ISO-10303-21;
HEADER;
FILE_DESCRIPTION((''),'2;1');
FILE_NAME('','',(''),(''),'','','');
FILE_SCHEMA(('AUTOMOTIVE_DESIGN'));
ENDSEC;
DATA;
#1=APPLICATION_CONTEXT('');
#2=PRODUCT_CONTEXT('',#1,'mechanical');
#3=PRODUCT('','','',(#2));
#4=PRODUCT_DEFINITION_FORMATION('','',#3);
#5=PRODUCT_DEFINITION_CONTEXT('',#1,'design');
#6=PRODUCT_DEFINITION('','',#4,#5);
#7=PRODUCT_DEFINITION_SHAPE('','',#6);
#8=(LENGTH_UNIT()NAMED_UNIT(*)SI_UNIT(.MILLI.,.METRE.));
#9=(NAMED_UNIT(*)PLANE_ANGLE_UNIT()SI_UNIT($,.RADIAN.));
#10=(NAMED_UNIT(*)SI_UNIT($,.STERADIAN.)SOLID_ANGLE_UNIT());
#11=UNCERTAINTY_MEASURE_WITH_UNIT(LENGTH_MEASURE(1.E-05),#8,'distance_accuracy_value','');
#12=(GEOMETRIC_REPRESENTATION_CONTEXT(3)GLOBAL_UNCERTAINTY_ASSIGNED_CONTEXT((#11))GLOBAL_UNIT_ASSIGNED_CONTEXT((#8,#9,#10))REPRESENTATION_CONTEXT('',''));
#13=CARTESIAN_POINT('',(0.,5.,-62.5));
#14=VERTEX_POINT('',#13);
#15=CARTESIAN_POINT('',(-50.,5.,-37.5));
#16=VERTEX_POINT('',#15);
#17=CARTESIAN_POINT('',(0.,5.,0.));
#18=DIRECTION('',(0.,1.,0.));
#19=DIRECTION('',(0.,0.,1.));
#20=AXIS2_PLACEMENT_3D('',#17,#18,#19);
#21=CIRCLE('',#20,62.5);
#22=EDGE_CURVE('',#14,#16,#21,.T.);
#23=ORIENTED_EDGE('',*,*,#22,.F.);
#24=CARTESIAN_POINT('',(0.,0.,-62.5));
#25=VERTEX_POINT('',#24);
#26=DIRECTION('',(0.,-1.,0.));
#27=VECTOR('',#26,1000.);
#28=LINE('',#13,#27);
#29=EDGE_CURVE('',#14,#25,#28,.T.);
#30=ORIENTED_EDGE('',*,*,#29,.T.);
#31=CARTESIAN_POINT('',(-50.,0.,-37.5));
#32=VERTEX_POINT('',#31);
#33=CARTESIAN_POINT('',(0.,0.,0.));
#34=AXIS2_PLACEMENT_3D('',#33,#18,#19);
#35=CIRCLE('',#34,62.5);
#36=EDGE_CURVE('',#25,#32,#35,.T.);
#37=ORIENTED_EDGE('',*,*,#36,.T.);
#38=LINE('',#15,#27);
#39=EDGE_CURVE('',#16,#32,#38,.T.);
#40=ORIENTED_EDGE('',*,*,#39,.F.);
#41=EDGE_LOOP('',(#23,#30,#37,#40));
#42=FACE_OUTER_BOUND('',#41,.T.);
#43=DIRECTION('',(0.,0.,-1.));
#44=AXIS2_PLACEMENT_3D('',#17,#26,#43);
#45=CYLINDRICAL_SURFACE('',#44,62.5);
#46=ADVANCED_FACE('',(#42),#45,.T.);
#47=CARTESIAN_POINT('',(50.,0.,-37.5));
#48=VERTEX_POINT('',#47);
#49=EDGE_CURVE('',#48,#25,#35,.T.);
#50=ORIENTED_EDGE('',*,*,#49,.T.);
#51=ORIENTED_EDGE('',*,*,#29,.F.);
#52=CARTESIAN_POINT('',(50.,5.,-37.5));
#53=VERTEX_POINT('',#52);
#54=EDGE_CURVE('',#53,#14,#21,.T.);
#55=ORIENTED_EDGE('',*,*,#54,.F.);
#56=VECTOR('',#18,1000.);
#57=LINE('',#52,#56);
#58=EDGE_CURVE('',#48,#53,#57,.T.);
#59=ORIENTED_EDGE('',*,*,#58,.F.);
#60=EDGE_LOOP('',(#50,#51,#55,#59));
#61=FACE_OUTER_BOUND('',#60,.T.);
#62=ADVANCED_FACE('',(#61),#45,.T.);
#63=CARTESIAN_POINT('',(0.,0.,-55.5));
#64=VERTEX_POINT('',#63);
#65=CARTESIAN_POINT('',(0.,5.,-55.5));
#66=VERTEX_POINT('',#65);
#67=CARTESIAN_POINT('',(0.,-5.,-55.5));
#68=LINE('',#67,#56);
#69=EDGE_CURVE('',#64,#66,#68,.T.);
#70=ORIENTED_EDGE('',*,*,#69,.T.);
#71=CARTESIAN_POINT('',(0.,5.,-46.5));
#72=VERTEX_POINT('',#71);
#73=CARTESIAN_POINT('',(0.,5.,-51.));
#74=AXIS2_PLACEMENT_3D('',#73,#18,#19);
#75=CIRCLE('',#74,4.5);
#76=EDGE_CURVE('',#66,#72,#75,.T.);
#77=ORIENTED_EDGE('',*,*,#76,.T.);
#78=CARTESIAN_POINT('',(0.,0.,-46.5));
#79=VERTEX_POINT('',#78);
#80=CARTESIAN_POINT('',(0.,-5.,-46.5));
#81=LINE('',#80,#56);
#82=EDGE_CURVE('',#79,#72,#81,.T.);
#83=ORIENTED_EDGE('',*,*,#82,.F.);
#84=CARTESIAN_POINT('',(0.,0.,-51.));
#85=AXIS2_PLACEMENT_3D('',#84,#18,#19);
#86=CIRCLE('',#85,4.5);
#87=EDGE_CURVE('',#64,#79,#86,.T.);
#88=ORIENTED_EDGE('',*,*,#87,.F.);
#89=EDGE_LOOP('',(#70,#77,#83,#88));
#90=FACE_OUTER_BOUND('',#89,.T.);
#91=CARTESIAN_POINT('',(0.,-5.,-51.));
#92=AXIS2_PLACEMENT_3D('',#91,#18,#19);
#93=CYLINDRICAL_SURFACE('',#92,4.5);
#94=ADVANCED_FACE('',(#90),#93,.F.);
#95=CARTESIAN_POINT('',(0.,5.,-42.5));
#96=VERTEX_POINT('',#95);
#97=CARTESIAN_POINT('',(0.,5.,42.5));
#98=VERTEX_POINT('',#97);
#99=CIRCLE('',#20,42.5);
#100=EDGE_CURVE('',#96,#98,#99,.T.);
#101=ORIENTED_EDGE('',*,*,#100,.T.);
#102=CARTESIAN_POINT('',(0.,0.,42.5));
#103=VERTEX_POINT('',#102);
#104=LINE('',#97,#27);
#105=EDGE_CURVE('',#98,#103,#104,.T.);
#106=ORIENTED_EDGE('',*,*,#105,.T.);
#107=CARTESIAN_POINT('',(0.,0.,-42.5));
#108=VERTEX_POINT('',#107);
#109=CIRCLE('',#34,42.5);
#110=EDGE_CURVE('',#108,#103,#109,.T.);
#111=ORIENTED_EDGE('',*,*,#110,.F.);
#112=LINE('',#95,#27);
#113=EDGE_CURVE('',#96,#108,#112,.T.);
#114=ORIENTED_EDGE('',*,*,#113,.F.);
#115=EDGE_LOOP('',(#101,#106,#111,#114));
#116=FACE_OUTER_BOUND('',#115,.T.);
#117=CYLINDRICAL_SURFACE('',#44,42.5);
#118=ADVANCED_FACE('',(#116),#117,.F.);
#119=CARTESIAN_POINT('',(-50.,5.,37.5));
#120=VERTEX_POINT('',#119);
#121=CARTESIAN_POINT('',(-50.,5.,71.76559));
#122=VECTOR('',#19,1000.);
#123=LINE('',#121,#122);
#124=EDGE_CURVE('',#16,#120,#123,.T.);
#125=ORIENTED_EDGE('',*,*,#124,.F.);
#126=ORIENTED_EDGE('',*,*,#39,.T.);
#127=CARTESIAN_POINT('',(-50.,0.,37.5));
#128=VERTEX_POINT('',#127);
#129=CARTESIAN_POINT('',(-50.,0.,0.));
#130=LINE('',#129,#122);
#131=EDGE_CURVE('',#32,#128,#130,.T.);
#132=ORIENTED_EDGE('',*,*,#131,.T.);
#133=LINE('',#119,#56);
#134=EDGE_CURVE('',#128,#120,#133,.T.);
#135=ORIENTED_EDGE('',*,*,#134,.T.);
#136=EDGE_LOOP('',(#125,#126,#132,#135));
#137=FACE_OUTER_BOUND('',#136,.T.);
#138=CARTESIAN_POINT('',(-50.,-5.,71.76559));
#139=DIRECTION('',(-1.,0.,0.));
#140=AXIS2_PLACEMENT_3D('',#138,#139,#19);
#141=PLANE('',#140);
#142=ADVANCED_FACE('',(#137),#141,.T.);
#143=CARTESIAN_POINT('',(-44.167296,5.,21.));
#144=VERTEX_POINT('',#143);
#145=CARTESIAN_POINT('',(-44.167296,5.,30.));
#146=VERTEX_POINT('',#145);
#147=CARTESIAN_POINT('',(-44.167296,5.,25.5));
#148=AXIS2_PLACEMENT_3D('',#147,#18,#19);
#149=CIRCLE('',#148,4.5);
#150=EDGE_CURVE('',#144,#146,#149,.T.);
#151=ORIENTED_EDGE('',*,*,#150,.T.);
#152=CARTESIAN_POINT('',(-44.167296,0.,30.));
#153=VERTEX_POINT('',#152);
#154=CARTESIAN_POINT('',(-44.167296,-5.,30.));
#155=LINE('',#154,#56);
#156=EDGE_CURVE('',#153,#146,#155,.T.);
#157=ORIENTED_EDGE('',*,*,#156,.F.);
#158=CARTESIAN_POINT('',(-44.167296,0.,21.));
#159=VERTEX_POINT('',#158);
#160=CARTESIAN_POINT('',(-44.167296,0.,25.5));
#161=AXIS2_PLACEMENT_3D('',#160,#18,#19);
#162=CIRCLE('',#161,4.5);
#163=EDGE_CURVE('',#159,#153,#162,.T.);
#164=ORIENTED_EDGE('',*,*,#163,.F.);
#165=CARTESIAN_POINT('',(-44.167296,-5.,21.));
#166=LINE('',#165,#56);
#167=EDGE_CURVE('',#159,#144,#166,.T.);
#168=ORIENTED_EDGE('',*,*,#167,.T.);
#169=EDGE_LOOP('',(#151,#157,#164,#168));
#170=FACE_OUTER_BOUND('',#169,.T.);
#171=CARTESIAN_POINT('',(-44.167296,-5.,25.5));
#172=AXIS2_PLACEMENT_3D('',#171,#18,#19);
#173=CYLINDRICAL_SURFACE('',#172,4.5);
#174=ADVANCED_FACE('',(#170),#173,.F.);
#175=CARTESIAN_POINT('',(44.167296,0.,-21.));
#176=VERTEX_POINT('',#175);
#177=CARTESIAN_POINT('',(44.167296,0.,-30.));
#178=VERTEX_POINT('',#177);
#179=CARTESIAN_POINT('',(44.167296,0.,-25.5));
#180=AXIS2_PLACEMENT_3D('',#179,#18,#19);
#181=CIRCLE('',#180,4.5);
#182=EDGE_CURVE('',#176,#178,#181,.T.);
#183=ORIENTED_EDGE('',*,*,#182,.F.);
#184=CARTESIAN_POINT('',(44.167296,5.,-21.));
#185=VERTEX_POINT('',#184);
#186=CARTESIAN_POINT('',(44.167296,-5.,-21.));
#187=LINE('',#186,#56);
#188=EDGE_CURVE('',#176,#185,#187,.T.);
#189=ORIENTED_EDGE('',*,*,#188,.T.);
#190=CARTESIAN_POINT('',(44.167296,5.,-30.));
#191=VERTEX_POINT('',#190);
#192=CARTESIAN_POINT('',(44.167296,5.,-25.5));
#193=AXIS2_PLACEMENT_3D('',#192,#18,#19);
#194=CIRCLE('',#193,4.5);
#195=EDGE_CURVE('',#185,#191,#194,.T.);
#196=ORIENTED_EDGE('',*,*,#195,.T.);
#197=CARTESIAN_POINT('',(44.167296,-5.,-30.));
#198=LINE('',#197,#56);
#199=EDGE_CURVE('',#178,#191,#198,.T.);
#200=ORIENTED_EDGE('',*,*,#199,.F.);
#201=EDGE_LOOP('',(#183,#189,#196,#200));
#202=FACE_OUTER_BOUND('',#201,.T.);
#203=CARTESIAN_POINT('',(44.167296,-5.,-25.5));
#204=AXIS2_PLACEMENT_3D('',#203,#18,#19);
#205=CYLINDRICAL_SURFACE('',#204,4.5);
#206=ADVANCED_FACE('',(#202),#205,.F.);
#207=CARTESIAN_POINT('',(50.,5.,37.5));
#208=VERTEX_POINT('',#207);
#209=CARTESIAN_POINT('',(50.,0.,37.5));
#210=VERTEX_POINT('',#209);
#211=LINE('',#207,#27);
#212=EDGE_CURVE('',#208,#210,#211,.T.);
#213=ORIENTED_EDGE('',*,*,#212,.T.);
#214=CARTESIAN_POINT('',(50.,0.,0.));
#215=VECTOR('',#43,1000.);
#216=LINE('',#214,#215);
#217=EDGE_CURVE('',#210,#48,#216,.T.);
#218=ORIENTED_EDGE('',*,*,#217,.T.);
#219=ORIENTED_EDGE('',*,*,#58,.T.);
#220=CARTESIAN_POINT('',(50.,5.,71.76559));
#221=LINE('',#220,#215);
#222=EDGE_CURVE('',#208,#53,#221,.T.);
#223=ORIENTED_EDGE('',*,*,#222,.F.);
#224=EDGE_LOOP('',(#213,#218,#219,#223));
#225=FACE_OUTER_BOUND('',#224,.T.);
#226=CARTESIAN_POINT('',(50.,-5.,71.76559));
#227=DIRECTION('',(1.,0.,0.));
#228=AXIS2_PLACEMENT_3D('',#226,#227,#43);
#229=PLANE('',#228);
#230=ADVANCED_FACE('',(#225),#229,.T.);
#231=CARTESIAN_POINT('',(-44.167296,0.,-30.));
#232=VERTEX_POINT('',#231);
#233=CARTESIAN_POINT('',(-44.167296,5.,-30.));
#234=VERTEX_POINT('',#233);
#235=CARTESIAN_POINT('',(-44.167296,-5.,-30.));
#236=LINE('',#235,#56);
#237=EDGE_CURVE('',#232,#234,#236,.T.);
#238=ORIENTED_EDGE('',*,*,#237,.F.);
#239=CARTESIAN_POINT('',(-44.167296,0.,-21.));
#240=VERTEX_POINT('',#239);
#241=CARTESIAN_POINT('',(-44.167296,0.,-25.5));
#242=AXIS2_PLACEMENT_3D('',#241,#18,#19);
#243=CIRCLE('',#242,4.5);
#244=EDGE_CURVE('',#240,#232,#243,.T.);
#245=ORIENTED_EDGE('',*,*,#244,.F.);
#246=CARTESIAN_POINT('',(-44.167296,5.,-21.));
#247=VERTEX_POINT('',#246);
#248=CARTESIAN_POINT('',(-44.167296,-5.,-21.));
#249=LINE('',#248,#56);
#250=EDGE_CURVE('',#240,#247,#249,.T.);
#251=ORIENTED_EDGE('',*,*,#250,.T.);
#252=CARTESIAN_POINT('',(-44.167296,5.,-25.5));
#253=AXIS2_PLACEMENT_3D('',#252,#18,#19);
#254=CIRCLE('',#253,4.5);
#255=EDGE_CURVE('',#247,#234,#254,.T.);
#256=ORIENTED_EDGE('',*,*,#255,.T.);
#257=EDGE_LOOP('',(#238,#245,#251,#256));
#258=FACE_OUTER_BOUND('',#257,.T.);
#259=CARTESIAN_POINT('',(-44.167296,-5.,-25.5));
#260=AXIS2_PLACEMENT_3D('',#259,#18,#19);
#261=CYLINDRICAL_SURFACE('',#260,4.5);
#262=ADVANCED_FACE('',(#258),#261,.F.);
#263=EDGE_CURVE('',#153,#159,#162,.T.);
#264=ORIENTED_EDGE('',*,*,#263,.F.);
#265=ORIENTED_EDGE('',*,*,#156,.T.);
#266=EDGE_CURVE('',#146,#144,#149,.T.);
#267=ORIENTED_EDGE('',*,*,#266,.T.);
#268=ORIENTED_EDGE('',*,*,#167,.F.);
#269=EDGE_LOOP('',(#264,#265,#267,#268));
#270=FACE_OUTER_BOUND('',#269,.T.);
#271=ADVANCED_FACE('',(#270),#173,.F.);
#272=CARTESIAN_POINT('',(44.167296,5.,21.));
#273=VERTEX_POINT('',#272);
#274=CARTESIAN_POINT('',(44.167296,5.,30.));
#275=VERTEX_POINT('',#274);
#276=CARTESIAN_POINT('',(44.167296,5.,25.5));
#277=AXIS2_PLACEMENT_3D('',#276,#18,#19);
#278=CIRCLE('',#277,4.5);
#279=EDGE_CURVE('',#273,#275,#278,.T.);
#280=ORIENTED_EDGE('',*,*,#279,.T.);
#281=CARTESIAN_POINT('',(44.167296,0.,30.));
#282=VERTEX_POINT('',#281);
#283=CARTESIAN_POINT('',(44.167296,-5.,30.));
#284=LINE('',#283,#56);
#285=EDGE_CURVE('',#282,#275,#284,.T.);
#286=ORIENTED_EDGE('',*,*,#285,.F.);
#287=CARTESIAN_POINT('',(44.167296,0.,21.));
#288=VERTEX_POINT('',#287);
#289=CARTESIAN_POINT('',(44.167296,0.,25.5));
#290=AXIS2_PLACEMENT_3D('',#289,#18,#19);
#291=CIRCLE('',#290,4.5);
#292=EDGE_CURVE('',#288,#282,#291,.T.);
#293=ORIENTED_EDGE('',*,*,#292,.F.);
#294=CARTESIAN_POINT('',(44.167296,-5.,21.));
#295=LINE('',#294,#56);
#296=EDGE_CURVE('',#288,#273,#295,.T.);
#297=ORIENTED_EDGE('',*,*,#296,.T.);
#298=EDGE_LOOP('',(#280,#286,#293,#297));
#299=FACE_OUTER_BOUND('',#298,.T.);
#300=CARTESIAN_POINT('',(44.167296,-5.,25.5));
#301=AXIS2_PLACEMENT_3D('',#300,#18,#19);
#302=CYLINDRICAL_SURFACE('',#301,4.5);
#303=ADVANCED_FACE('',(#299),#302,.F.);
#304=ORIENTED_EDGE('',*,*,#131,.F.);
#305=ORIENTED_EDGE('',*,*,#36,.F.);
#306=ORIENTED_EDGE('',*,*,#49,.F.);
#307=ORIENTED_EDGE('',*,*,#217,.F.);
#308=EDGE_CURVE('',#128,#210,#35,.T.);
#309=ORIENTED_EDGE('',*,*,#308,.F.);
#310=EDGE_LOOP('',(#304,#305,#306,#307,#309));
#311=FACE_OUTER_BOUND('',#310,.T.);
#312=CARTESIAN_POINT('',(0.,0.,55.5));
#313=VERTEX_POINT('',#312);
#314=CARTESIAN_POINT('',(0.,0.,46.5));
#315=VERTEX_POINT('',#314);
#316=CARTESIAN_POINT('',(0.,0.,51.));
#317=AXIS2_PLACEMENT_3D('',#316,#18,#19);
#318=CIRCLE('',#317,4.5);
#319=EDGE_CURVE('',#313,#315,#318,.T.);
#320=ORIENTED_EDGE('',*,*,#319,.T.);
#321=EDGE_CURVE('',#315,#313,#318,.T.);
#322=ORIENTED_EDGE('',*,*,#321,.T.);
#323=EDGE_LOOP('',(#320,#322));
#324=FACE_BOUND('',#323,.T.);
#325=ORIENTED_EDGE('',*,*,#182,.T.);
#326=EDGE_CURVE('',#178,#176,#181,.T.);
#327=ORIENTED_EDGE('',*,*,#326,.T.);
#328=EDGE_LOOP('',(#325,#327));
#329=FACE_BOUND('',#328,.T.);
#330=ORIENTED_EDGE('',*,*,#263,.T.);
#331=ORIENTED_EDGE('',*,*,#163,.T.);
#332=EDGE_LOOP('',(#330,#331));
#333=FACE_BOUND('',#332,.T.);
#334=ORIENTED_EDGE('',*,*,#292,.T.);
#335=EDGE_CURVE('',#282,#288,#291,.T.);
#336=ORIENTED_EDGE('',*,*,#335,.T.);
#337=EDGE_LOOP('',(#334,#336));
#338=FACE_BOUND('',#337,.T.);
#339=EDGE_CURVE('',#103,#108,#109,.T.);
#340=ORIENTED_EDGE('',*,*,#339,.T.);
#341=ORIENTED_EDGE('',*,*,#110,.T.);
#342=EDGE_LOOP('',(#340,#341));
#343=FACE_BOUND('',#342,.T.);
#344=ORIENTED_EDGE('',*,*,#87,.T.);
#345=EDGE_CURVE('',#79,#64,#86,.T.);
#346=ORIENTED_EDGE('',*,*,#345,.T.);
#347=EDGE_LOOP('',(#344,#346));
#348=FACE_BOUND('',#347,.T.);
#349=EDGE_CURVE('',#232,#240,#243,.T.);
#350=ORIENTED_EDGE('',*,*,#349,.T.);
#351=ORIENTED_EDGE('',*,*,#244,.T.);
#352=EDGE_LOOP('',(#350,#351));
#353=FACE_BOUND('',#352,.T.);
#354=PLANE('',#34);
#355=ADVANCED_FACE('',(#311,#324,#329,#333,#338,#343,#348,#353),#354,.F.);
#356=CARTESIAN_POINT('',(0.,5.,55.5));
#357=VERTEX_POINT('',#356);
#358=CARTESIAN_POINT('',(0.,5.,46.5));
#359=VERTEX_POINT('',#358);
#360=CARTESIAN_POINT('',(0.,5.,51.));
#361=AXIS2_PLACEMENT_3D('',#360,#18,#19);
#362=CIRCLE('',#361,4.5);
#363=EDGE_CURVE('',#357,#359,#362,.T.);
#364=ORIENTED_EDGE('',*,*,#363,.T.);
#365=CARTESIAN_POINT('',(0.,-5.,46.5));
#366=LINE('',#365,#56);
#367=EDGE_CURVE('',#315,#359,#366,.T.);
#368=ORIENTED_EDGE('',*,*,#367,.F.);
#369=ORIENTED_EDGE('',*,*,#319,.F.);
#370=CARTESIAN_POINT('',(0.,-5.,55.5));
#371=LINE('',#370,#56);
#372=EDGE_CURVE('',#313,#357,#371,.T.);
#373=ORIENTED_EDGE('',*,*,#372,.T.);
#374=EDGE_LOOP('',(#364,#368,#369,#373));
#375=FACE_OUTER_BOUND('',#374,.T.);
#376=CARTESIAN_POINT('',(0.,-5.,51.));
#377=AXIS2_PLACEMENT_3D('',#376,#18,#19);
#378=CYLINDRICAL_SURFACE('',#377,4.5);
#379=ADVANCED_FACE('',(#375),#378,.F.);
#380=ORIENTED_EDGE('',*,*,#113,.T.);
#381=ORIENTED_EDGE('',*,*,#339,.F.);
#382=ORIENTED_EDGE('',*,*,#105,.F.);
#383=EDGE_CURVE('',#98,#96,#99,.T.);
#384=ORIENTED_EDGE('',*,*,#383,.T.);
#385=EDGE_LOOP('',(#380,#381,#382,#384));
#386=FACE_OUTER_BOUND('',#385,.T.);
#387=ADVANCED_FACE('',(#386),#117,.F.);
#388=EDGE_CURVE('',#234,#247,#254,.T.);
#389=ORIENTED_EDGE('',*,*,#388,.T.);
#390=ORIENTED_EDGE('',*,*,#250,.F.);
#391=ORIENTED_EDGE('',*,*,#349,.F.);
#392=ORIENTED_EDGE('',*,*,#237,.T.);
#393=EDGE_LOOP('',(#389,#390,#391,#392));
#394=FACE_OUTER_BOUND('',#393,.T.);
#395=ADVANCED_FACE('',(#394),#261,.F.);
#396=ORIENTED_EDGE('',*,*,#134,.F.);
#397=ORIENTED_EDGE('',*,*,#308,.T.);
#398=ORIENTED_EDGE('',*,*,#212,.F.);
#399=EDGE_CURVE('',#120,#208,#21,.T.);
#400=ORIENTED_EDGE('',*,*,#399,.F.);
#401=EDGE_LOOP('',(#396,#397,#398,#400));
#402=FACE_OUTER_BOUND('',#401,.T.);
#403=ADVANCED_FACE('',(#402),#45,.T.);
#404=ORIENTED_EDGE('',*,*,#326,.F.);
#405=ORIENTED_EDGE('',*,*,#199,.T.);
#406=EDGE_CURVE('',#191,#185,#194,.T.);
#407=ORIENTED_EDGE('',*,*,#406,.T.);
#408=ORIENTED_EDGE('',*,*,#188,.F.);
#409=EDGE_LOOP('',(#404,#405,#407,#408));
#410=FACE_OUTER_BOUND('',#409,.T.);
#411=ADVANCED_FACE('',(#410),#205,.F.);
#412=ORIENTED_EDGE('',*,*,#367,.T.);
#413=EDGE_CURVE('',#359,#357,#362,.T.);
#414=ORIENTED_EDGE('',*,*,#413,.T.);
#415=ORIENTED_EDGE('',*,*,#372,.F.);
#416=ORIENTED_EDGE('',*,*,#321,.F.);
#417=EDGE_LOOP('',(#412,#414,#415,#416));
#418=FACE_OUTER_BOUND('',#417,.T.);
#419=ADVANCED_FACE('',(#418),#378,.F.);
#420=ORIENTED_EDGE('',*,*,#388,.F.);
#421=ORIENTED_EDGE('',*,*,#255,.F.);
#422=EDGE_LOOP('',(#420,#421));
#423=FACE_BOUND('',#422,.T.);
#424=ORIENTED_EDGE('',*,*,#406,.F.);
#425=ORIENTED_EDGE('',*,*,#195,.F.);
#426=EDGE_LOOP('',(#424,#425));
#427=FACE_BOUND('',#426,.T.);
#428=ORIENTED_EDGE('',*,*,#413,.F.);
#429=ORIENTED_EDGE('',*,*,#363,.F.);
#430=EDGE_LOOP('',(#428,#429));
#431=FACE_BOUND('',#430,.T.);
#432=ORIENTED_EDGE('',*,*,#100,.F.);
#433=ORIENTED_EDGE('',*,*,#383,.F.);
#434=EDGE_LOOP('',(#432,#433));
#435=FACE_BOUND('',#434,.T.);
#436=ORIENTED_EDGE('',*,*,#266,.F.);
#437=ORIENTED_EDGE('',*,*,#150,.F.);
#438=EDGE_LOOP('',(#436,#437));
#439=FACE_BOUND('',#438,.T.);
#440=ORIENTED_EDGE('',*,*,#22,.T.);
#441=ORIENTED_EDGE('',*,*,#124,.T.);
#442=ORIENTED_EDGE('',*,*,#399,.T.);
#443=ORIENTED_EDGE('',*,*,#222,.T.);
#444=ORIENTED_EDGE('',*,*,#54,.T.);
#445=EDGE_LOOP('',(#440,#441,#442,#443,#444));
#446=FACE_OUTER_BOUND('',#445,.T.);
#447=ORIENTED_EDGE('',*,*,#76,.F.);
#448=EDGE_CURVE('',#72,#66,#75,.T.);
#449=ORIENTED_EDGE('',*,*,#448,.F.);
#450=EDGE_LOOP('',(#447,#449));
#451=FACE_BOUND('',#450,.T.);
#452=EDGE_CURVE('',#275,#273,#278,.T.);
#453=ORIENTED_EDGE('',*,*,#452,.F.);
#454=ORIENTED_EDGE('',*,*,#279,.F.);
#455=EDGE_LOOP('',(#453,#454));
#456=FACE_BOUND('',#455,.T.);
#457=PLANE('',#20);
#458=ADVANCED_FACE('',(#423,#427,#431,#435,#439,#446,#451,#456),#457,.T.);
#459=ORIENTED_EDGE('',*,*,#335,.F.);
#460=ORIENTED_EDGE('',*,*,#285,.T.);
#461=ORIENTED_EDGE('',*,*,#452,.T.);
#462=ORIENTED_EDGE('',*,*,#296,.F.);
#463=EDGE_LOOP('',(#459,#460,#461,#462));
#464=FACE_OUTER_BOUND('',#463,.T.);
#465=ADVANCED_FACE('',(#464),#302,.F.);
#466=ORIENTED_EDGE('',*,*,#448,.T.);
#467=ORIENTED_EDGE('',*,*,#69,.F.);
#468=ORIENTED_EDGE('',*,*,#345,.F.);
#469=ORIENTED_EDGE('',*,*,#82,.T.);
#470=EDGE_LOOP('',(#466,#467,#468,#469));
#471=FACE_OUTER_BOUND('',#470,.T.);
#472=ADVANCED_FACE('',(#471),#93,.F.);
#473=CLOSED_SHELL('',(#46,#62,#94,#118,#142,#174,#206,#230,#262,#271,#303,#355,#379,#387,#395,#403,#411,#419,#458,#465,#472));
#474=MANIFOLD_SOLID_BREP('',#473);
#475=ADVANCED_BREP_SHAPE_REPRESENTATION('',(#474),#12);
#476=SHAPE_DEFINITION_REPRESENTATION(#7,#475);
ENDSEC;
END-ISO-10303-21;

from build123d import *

# Parameters (mm, degrees)
SKETCH1_R           = 62.5
SKETCH1_R_2         = 42.5
BOSS_EXTRUDE1_DEPTH = 5
SKETCH2_R           = 4.5
CUT_EXTRUDE1_DEPTH  = 10
SKETCH3_OUTSIDE_W   = 162.37
SKETCH3_OUTSIDE_H   = 162.37
SKETCH3_OUTSIDE_W_2 = 100
SKETCH3_OUTSIDE_H_2 = 143.531180288
CUT_EXTRUDE2_DEPTH  = 10


with BuildPart() as part:
    # Sketch1 → Boss-Extrude1 (new body)
    with BuildSketch(Plane(origin=(0, 0, 0), x_dir=(1, 0, 0), z_dir=(0, 1, 0))):
        with Locations(Location((0, 0, 0), (0, 0, 270))):
            Circle(SKETCH1_R)
        with Locations(Location((0, 0, 0), (0, 0, 270))):
            Circle(SKETCH1_R_2, mode=Mode.SUBTRACT)
    extrude(amount=BOSS_EXTRUDE1_DEPTH)

    # Sketch2 → Cut-Extrude1 (cut)
    with BuildSketch(Plane(origin=(0, 5, 0), x_dir=(1, 0, 0), z_dir=(0, 1, 0))):
        with Locations(Location((0, 51, 0), (0, 0, 270))):
            Circle(SKETCH2_R)
        with Locations(Location((44.167295593, 25.5, 0), (0, 0, 270))):
            Circle(SKETCH2_R)
        with Locations(Location((44.167295593, -25.5, 0), (0, 0, 270))):
            Circle(SKETCH2_R)
        with Locations(Location((0, -51, 0), (0, 0, 270))):
            Circle(SKETCH2_R)
        with Locations(Location((-44.167295593, -25.5, 0), (0, 0, 270))):
            Circle(SKETCH2_R)
        with Locations(Location((-44.167295593, 25.5, 0), (0, 0, 270))):
            Circle(SKETCH2_R)
    extrude(amount=-CUT_EXTRUDE1_DEPTH, mode=Mode.SUBTRACT)

    # Sketch3 outside → Cut-Extrude2 (cut)
    with BuildSketch(Plane(origin=(0, 5, 0), x_dir=(1, 0, 0), z_dir=(0, 1, 0))):
        Rectangle(SKETCH3_OUTSIDE_W, SKETCH3_OUTSIDE_H)
        Rectangle(SKETCH3_OUTSIDE_W_2, SKETCH3_OUTSIDE_H_2, mode=Mode.SUBTRACT)
    extrude(amount=-CUT_EXTRUDE2_DEPTH, mode=Mode.SUBTRACT)


solid = part.part
